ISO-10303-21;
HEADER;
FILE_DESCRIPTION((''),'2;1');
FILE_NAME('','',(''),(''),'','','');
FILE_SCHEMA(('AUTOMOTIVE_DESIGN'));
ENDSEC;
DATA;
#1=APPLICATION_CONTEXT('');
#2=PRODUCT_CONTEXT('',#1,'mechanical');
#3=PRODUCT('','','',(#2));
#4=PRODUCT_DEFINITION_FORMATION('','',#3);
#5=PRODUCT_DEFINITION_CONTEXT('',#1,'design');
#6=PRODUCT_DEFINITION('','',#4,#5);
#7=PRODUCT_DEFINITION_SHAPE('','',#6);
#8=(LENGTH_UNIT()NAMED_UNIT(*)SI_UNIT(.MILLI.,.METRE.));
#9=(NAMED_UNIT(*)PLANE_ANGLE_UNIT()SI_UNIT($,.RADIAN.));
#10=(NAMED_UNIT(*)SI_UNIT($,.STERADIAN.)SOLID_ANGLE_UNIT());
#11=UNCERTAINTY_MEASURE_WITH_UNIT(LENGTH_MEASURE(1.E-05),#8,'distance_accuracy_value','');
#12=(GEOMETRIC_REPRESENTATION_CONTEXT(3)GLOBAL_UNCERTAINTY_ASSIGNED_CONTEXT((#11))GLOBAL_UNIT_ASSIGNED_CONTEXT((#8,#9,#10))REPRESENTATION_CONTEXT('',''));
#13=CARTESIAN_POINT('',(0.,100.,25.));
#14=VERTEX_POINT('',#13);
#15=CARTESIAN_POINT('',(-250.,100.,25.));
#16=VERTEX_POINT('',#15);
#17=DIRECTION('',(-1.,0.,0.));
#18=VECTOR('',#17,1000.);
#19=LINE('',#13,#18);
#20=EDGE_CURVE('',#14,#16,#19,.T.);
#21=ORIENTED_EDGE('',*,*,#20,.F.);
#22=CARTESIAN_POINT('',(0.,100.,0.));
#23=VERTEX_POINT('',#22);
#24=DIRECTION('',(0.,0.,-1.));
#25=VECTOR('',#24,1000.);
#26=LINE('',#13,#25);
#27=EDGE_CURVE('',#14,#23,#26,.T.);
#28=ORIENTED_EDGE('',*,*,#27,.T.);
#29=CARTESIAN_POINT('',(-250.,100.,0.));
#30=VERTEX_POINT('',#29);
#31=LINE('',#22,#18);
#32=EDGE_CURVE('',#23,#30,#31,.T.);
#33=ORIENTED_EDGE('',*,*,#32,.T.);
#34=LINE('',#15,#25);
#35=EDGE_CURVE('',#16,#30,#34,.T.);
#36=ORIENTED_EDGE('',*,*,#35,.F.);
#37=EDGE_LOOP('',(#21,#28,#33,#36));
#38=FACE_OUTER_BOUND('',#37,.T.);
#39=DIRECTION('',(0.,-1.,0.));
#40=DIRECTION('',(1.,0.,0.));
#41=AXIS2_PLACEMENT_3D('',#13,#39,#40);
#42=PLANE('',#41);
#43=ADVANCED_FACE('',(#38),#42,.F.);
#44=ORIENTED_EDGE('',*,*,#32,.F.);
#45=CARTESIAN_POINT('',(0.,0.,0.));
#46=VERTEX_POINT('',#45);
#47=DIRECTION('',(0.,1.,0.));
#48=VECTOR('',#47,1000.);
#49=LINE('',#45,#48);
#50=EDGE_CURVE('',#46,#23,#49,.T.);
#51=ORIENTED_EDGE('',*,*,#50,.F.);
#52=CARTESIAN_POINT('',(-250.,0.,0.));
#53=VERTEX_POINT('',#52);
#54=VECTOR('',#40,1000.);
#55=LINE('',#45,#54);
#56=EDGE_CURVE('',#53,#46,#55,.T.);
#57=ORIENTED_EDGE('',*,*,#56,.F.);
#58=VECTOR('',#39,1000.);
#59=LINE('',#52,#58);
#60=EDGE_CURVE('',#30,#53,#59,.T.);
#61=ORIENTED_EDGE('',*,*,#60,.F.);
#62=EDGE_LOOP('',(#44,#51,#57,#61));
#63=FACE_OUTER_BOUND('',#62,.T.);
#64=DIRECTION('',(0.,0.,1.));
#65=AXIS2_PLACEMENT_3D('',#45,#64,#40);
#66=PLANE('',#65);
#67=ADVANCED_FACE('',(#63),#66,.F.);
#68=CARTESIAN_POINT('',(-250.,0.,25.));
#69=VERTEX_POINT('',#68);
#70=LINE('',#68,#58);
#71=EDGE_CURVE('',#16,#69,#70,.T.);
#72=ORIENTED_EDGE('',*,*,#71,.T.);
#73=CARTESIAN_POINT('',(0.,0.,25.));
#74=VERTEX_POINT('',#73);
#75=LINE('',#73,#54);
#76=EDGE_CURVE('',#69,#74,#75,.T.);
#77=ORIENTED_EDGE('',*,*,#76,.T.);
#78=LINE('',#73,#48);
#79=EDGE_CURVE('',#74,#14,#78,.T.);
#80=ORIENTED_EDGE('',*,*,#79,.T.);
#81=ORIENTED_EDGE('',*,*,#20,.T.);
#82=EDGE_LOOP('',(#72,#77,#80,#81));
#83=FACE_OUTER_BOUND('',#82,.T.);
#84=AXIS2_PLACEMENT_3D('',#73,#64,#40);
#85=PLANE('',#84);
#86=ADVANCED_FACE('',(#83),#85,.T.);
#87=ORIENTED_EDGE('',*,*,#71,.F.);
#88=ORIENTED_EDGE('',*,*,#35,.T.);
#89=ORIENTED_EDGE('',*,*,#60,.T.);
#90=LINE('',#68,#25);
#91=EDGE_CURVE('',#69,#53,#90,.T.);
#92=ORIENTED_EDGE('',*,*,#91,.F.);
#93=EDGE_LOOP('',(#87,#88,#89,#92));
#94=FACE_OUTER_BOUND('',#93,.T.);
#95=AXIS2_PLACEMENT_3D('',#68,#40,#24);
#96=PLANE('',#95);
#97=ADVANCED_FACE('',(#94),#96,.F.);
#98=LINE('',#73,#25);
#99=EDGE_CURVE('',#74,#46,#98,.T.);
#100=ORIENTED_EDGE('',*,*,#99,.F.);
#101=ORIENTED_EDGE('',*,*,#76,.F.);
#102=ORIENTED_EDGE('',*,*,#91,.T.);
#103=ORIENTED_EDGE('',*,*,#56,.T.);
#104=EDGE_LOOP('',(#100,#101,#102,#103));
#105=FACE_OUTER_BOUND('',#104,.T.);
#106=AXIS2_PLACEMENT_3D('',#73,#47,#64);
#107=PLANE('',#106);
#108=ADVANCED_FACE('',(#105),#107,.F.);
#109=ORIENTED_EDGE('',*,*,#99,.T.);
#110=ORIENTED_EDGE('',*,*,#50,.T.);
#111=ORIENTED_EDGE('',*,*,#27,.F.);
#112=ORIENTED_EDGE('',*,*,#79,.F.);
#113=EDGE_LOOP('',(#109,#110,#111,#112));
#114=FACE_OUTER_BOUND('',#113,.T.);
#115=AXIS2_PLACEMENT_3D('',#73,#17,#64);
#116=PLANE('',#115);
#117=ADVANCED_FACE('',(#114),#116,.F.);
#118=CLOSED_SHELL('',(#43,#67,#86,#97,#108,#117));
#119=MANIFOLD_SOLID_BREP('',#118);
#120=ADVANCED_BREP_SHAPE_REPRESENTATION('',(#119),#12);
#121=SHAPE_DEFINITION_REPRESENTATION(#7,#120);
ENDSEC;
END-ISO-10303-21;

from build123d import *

# Parameters (mm, degrees)
SKETCH1_W           = 250
SKETCH1_H           = 100
BOSS_EXTRUDE1_DEPTH = 25


with BuildPart() as part:
    # Sketch1 → Boss-Extrude1 (new body)
    with BuildSketch(Plane.XY):
        with Locations((-125, 50)):
            Rectangle(SKETCH1_W, SKETCH1_H)
    extrude(amount=BOSS_EXTRUDE1_DEPTH)


solid = part.part
